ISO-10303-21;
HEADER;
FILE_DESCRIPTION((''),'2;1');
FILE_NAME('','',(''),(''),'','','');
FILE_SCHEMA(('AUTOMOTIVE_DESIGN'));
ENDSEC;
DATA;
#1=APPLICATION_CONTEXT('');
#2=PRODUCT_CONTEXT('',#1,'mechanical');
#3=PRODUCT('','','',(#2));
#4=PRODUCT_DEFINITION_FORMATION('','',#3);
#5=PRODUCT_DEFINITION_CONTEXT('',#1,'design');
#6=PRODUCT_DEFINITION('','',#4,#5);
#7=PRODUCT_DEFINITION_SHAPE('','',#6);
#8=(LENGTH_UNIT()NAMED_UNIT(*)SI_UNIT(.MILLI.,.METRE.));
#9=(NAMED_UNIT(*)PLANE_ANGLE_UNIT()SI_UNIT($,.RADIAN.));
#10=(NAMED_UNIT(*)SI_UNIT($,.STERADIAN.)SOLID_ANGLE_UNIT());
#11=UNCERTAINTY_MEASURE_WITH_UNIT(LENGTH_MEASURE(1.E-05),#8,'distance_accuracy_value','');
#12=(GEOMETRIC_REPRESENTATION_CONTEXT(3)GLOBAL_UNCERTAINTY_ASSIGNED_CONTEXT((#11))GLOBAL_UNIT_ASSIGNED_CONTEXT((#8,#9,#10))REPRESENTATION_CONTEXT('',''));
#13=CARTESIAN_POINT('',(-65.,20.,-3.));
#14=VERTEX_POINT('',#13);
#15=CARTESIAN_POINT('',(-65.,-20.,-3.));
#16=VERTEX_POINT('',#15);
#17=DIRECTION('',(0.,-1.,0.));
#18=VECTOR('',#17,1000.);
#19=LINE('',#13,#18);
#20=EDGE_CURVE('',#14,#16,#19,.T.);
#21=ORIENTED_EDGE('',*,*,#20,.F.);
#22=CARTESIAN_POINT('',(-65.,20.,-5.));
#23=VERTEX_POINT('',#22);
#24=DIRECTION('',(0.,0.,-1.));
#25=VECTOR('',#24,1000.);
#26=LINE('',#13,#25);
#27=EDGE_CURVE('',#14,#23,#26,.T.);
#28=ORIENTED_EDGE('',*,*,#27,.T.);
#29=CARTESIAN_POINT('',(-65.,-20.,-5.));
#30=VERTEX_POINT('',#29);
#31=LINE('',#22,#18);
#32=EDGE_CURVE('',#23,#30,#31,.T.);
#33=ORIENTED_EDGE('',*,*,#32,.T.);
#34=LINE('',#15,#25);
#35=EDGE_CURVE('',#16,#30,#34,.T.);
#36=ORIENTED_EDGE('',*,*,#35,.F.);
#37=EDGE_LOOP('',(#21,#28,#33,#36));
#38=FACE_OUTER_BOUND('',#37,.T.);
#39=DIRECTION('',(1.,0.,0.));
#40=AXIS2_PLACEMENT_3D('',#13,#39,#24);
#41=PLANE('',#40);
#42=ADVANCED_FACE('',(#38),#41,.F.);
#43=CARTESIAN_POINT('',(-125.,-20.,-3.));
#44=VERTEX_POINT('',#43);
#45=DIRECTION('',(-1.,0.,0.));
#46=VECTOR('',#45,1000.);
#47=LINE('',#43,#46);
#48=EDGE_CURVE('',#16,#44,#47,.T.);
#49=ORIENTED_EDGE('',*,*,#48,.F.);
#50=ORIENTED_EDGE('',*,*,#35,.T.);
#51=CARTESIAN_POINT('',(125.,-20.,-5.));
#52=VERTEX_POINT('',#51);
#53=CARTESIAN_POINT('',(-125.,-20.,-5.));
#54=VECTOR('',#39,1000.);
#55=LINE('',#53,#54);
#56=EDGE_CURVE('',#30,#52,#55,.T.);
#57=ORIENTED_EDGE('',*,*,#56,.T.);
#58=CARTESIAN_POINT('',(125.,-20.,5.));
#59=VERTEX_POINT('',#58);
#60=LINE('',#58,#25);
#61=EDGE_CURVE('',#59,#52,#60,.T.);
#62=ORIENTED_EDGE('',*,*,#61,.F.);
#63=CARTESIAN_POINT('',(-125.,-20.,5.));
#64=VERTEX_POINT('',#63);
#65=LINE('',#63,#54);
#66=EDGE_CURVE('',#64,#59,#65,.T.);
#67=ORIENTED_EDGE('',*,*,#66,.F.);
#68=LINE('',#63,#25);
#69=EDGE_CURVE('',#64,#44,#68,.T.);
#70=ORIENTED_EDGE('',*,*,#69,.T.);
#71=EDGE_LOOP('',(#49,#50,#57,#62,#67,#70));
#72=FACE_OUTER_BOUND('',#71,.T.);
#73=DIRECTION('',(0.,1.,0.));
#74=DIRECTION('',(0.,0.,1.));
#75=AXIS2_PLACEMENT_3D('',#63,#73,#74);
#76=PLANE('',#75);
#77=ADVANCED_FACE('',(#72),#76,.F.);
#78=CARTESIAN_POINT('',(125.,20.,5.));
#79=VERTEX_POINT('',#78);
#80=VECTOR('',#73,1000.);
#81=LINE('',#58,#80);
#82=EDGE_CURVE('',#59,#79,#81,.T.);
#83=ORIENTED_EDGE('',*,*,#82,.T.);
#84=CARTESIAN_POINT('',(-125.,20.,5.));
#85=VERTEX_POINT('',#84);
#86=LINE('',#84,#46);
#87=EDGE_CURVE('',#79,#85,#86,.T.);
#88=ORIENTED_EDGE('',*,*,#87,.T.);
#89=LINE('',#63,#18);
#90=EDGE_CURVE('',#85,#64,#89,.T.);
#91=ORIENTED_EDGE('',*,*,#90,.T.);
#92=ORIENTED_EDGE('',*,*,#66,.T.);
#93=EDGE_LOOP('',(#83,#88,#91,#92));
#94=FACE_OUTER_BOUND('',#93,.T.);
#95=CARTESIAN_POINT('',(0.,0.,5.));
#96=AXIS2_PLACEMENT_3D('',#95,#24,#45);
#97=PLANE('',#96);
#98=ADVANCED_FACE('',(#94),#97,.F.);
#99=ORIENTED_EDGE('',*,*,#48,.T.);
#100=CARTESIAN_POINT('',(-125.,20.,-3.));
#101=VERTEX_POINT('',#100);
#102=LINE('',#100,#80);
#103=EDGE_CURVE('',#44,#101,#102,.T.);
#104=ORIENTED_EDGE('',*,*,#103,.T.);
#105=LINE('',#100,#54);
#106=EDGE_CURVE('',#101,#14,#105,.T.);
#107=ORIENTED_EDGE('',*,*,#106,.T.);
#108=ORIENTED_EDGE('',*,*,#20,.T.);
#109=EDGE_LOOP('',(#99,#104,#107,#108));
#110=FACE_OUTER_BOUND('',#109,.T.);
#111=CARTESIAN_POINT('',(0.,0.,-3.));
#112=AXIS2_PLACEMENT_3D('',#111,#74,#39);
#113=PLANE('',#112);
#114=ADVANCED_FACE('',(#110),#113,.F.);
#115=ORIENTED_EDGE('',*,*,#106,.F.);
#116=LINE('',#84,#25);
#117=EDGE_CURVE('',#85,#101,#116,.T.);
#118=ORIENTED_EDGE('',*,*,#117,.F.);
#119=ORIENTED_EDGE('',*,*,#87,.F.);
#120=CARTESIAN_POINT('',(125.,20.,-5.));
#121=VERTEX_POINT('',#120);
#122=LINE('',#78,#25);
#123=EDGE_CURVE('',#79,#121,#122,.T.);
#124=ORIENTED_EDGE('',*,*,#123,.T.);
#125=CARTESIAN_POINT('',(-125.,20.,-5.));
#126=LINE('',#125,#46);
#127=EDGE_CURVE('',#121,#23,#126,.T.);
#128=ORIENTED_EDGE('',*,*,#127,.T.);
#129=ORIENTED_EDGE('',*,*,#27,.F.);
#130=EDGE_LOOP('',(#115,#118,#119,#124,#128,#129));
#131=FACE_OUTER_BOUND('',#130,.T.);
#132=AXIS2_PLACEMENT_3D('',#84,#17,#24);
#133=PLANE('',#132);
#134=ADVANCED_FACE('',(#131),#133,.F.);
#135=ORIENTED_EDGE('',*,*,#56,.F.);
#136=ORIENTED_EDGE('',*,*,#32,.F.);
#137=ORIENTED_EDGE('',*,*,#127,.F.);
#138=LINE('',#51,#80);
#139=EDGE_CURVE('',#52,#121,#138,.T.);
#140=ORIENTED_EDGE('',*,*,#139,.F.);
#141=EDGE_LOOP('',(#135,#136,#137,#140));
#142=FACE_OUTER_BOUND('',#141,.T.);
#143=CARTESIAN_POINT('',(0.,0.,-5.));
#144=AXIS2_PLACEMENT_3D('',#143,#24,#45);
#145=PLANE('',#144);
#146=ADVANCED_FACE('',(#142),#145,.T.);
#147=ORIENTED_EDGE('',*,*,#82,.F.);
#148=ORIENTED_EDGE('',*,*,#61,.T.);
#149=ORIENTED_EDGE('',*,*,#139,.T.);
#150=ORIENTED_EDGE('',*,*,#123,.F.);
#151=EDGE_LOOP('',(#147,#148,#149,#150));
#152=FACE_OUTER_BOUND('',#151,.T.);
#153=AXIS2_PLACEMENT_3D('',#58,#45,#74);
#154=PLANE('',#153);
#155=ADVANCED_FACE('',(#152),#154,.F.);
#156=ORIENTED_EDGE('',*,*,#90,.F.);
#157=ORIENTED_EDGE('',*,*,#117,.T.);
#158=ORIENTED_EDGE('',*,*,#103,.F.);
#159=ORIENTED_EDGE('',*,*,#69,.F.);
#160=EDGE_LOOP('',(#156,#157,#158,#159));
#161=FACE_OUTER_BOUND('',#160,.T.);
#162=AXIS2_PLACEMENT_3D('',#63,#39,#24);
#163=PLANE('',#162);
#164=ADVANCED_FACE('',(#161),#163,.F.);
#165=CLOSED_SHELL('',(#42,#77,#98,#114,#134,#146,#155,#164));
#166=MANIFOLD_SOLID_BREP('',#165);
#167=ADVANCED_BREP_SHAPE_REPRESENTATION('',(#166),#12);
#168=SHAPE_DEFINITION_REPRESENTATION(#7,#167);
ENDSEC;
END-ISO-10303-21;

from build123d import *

# Parameters (mm, degrees)
SKETCH_1_W          = 250
SKETCH_1_H          = 40
EXTRUDE_1_DEPTH     = 5
SKETCH_2_W          = 60
SKETCH_2_H          = 40
CUT_EXTRUDE_1_DEPTH = 2


with BuildPart() as part:
    # 草图1 → 凸台-拉伸1 (new, symmetric)
    with BuildSketch(Plane.XY):
        Rectangle(SKETCH_1_W, SKETCH_1_H)
    extrude(amount=EXTRUDE_1_DEPTH, both=True)

    # 草图2 → 切除-拉伸1 (cut)
    with BuildSketch(Plane(origin=(0, 0, -5), x_dir=(-1, 0, 0), z_dir=(0, 0, -1))):
        with Locations((95, 0)):
            Rectangle(SKETCH_2_W, SKETCH_2_H)
    extrude(amount=-CUT_EXTRUDE_1_DEPTH, mode=Mode.SUBTRACT)


solid = part.part
